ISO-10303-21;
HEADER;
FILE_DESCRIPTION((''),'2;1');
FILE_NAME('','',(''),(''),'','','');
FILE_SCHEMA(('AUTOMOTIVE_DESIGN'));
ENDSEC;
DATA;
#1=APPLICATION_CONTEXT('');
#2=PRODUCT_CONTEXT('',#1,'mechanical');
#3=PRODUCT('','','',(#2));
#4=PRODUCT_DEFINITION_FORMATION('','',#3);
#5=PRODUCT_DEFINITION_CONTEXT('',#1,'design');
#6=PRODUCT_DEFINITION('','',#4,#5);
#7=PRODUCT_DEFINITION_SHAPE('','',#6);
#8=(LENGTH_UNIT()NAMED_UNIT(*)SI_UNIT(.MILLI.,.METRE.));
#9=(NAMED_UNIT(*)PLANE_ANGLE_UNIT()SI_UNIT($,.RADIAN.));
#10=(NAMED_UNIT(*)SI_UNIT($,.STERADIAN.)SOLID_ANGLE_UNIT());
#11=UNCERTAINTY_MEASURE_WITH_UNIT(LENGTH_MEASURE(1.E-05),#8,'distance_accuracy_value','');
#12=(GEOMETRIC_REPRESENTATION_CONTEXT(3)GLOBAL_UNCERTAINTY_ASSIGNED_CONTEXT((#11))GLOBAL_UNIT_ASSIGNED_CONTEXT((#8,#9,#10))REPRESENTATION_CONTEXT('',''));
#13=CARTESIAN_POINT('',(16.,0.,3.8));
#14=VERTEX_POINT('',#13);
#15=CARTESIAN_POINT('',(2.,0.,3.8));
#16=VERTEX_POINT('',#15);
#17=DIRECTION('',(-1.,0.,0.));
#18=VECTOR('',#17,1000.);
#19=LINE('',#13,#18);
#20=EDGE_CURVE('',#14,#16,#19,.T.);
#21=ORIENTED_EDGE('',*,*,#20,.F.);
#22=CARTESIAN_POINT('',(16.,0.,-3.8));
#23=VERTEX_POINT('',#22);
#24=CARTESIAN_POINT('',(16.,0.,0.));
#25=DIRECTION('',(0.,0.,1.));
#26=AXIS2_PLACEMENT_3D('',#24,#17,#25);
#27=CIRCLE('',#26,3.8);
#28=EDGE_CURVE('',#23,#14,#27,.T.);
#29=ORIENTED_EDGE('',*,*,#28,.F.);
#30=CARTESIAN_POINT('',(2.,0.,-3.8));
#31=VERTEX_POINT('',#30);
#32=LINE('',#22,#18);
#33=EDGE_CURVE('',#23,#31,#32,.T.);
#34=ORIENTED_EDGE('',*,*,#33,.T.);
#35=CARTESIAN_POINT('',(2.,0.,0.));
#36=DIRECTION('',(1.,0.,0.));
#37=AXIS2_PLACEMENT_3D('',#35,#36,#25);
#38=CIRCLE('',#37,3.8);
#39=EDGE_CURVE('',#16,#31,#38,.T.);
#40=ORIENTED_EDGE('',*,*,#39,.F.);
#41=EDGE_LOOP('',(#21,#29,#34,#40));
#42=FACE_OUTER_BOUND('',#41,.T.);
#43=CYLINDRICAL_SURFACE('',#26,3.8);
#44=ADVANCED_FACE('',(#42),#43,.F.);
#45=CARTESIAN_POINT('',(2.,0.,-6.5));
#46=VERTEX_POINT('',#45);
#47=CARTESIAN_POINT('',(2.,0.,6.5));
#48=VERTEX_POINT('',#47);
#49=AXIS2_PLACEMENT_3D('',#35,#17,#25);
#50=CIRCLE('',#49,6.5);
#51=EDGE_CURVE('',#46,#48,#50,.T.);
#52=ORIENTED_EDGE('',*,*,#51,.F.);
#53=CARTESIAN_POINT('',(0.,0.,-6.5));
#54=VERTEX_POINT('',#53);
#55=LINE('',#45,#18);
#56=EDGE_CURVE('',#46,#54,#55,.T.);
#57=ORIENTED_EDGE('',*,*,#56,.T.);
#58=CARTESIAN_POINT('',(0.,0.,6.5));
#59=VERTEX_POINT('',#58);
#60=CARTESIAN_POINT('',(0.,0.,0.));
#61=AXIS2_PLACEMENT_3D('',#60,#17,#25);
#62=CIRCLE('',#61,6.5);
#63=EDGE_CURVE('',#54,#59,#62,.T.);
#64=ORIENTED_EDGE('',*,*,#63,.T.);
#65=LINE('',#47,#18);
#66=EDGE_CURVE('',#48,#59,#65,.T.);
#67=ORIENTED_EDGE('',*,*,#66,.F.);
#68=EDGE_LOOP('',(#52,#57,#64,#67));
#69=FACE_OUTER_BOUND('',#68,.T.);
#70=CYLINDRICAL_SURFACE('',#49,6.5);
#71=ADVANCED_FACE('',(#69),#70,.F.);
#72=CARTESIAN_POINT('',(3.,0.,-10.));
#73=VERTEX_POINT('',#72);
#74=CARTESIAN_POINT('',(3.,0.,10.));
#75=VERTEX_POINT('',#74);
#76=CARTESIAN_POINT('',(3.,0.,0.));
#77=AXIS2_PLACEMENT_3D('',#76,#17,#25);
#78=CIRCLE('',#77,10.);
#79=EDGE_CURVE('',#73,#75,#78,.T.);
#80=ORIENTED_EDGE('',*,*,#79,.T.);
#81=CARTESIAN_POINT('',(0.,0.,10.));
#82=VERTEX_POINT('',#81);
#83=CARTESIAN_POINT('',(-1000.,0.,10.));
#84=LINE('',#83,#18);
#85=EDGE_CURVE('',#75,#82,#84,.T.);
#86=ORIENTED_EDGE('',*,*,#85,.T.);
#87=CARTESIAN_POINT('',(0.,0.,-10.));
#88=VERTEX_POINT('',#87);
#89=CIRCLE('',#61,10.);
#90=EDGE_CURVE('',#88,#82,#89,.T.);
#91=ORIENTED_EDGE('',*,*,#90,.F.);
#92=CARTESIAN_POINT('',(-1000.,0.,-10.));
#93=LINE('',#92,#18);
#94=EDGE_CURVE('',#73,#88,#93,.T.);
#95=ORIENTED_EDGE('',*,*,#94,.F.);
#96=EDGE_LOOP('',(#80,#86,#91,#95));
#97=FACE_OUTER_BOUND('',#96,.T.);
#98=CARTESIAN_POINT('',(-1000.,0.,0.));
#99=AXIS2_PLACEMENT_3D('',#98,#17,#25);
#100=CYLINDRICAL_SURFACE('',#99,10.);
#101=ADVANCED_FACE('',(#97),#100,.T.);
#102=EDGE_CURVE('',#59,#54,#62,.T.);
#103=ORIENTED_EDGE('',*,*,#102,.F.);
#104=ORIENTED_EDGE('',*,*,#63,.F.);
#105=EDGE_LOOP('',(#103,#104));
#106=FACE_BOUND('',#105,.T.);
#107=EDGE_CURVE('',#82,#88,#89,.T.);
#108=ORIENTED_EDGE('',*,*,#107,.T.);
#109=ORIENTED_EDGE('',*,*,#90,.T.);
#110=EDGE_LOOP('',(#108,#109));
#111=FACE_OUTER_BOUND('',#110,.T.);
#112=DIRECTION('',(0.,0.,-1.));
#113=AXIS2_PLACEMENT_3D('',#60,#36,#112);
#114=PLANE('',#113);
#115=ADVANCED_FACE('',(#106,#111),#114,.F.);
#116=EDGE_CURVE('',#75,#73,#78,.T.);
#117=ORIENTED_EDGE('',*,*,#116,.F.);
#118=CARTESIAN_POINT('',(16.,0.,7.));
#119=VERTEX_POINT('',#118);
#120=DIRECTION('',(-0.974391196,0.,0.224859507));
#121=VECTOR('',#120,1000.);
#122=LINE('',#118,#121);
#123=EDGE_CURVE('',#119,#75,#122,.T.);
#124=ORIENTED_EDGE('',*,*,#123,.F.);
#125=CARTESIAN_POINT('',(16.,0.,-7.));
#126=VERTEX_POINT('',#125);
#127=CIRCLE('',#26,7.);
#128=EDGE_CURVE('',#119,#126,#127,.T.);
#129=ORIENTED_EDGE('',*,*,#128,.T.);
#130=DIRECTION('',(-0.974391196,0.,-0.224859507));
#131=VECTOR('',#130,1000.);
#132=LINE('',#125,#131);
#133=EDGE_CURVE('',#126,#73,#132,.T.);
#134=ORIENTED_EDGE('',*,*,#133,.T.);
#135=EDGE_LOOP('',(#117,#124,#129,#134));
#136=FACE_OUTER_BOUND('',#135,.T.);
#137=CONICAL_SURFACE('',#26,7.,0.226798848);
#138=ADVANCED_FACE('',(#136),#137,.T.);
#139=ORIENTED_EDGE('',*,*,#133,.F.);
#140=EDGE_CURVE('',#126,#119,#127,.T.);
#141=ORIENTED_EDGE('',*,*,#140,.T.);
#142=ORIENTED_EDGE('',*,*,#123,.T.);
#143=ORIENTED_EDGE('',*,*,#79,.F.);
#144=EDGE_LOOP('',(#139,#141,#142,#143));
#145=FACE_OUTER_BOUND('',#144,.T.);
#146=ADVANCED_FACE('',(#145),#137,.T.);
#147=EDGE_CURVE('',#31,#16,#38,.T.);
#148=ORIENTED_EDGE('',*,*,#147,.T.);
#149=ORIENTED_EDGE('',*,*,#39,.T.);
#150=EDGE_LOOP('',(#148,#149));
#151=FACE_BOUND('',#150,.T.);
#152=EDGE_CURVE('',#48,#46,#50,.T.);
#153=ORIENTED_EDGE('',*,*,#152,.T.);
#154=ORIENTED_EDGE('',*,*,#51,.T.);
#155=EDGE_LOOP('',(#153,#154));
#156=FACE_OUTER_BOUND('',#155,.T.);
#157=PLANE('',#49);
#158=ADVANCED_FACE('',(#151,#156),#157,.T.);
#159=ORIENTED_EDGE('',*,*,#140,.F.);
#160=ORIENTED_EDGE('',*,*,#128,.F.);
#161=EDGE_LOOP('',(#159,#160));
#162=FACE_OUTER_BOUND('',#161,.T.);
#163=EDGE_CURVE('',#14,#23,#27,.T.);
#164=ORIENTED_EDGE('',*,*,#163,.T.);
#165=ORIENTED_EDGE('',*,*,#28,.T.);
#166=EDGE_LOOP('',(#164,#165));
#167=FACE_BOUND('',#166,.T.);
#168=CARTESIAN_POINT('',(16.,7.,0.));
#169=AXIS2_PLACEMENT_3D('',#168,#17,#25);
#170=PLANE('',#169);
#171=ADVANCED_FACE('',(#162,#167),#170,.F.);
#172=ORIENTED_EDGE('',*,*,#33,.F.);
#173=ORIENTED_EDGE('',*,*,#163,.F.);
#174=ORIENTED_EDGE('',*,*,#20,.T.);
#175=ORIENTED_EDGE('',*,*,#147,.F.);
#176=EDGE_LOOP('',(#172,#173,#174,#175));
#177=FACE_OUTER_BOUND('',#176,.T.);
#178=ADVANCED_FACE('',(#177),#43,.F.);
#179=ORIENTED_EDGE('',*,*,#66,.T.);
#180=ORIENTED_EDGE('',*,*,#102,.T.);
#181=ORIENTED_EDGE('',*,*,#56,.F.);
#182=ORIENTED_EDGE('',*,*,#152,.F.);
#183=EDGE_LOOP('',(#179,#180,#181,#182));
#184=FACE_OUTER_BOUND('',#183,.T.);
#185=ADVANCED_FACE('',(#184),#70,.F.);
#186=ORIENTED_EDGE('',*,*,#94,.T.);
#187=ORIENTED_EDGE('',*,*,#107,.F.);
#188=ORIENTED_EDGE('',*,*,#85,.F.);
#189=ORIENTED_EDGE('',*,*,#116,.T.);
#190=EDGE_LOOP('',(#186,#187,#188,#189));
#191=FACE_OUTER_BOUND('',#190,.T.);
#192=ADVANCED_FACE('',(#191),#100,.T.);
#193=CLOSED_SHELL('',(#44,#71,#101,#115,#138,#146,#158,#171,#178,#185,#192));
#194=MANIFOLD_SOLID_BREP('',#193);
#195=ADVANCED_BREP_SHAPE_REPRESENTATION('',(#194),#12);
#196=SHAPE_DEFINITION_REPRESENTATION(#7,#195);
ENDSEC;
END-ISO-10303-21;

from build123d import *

# Parameters (mm, degrees)
BORE_SKETCH_R      = 3.8
THROUGH_BORE_DEPTH = 22.354156504
RECESS_SKETCH_13_R = 6.5
RECESS_13X2_DEPTH  = 2


with BuildPart() as part:
    # Bush Profile Sketch → Bush Body (revolve)
    with BuildSketch(Plane.XY, mode=Mode.PRIVATE) as bush_body_sk:
        Polygon((0, 0), (0, 10), (3, 10), (16, 7), (16, 0), align=None)
    revolve(bush_body_sk.sketch.rotate(Axis((-1000, 0, 0), (1, 0, 0)), 90), axis=Axis((-1000, 0, 0), (1, 0, 0)))

    # Bore Sketch → Through Bore (cut, through all)
    with BuildSketch(Plane.ZY):
        Circle(BORE_SKETCH_R)
    extrude(amount=-THROUGH_BORE_DEPTH, mode=Mode.SUBTRACT)

    # Recess Sketch Ø13 → Recess Ø13x2 (cut)
    with BuildSketch(Plane.ZY):
        Circle(RECESS_SKETCH_13_R)
    extrude(amount=-RECESS_13X2_DEPTH, mode=Mode.SUBTRACT)


solid = part.part
